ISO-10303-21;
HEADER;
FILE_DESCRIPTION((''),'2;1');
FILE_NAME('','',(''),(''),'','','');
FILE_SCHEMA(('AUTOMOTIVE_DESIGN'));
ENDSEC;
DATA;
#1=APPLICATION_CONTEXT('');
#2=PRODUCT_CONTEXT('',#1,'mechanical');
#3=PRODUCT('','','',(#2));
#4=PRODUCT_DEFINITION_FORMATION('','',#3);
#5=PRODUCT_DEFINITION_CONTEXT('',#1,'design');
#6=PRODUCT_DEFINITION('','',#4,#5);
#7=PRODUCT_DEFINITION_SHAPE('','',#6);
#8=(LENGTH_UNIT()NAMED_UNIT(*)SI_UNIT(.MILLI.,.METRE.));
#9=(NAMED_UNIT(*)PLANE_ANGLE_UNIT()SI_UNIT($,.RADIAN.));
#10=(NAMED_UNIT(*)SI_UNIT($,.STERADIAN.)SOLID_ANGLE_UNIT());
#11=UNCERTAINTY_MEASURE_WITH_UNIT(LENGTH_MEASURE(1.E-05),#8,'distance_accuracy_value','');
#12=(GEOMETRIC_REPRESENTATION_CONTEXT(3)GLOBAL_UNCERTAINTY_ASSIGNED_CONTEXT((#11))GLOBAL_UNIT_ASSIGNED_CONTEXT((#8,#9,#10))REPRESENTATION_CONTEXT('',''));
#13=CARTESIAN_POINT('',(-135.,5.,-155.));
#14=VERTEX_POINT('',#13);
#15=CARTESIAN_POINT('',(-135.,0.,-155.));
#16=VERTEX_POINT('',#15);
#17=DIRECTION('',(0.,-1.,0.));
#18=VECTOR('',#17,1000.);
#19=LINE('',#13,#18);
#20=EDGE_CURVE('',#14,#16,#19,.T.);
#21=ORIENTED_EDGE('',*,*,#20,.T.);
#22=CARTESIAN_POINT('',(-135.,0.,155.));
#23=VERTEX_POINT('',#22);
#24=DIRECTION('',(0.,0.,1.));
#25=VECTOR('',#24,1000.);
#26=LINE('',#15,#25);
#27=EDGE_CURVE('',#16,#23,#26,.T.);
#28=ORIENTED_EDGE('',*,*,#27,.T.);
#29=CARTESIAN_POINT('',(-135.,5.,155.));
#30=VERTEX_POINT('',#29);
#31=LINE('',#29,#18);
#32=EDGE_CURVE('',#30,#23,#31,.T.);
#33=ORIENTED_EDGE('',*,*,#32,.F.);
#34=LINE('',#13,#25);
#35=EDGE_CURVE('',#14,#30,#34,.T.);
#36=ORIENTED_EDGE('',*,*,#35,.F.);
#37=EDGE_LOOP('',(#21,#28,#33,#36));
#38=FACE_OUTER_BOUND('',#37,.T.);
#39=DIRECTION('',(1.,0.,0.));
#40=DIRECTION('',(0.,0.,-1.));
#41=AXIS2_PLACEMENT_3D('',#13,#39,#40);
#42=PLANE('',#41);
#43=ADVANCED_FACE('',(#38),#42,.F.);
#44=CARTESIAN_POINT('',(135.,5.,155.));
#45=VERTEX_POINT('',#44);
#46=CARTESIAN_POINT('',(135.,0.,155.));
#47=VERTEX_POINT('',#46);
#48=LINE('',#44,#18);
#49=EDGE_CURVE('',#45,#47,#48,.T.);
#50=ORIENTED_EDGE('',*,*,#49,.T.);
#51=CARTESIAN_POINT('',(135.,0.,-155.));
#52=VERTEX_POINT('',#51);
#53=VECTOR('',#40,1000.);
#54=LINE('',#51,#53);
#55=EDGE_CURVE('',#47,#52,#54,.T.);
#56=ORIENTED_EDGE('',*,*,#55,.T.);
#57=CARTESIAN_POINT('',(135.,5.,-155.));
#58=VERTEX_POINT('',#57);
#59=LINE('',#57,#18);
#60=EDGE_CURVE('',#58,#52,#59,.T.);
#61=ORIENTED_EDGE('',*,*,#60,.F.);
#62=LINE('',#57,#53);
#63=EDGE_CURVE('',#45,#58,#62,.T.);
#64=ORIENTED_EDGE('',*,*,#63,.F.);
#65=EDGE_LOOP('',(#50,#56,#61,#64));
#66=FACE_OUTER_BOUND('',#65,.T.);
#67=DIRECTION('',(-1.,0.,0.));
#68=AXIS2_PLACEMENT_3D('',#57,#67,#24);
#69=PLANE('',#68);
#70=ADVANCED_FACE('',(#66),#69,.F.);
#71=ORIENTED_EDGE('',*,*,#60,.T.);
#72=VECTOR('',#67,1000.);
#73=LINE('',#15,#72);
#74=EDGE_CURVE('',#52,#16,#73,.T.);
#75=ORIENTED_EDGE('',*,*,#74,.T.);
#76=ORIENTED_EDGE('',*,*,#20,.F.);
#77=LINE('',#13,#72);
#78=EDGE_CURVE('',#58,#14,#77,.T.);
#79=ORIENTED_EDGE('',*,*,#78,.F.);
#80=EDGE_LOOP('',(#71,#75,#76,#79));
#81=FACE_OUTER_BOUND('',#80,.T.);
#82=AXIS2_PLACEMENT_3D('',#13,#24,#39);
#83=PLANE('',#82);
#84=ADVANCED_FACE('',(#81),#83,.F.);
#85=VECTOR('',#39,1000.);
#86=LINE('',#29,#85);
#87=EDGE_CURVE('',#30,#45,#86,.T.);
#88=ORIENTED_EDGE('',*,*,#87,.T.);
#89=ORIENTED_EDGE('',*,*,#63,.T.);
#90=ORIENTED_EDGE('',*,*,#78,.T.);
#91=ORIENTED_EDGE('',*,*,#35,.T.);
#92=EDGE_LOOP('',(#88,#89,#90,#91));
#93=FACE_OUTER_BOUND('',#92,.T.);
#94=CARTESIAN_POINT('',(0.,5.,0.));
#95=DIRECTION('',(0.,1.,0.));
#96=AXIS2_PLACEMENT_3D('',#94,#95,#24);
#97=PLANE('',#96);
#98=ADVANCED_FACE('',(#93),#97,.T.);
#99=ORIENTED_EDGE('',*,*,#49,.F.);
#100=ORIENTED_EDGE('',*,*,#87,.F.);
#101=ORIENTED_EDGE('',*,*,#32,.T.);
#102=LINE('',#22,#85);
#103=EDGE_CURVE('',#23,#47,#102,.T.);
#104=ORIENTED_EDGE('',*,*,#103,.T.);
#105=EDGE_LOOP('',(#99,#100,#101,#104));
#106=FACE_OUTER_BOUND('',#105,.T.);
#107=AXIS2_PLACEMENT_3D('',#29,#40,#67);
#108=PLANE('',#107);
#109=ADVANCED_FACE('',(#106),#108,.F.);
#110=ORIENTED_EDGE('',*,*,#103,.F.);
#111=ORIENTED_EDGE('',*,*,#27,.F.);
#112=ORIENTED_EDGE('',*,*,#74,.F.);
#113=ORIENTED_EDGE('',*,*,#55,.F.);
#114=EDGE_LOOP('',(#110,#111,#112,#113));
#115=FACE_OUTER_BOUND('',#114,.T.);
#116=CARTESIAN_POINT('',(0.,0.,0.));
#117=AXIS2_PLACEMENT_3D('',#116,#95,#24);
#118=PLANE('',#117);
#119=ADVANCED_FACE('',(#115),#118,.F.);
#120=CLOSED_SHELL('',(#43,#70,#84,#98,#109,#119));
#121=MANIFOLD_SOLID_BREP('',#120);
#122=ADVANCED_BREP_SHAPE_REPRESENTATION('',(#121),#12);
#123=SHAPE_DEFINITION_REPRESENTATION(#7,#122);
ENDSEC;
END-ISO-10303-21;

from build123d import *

# Parameters (mm, degrees)
SKETCH1_W           = 270
SKETCH1_H           = 310
BOSS_EXTRUDE1_DEPTH = 5


with BuildPart() as part:
    # Sketch1 → Boss-Extrude1 (new body)
    with BuildSketch(Plane(origin=(0, 0, 0), x_dir=(1, 0, 0), z_dir=(0, 1, 0))):
        Rectangle(SKETCH1_W, SKETCH1_H)
    extrude(amount=BOSS_EXTRUDE1_DEPTH)


solid = part.part
